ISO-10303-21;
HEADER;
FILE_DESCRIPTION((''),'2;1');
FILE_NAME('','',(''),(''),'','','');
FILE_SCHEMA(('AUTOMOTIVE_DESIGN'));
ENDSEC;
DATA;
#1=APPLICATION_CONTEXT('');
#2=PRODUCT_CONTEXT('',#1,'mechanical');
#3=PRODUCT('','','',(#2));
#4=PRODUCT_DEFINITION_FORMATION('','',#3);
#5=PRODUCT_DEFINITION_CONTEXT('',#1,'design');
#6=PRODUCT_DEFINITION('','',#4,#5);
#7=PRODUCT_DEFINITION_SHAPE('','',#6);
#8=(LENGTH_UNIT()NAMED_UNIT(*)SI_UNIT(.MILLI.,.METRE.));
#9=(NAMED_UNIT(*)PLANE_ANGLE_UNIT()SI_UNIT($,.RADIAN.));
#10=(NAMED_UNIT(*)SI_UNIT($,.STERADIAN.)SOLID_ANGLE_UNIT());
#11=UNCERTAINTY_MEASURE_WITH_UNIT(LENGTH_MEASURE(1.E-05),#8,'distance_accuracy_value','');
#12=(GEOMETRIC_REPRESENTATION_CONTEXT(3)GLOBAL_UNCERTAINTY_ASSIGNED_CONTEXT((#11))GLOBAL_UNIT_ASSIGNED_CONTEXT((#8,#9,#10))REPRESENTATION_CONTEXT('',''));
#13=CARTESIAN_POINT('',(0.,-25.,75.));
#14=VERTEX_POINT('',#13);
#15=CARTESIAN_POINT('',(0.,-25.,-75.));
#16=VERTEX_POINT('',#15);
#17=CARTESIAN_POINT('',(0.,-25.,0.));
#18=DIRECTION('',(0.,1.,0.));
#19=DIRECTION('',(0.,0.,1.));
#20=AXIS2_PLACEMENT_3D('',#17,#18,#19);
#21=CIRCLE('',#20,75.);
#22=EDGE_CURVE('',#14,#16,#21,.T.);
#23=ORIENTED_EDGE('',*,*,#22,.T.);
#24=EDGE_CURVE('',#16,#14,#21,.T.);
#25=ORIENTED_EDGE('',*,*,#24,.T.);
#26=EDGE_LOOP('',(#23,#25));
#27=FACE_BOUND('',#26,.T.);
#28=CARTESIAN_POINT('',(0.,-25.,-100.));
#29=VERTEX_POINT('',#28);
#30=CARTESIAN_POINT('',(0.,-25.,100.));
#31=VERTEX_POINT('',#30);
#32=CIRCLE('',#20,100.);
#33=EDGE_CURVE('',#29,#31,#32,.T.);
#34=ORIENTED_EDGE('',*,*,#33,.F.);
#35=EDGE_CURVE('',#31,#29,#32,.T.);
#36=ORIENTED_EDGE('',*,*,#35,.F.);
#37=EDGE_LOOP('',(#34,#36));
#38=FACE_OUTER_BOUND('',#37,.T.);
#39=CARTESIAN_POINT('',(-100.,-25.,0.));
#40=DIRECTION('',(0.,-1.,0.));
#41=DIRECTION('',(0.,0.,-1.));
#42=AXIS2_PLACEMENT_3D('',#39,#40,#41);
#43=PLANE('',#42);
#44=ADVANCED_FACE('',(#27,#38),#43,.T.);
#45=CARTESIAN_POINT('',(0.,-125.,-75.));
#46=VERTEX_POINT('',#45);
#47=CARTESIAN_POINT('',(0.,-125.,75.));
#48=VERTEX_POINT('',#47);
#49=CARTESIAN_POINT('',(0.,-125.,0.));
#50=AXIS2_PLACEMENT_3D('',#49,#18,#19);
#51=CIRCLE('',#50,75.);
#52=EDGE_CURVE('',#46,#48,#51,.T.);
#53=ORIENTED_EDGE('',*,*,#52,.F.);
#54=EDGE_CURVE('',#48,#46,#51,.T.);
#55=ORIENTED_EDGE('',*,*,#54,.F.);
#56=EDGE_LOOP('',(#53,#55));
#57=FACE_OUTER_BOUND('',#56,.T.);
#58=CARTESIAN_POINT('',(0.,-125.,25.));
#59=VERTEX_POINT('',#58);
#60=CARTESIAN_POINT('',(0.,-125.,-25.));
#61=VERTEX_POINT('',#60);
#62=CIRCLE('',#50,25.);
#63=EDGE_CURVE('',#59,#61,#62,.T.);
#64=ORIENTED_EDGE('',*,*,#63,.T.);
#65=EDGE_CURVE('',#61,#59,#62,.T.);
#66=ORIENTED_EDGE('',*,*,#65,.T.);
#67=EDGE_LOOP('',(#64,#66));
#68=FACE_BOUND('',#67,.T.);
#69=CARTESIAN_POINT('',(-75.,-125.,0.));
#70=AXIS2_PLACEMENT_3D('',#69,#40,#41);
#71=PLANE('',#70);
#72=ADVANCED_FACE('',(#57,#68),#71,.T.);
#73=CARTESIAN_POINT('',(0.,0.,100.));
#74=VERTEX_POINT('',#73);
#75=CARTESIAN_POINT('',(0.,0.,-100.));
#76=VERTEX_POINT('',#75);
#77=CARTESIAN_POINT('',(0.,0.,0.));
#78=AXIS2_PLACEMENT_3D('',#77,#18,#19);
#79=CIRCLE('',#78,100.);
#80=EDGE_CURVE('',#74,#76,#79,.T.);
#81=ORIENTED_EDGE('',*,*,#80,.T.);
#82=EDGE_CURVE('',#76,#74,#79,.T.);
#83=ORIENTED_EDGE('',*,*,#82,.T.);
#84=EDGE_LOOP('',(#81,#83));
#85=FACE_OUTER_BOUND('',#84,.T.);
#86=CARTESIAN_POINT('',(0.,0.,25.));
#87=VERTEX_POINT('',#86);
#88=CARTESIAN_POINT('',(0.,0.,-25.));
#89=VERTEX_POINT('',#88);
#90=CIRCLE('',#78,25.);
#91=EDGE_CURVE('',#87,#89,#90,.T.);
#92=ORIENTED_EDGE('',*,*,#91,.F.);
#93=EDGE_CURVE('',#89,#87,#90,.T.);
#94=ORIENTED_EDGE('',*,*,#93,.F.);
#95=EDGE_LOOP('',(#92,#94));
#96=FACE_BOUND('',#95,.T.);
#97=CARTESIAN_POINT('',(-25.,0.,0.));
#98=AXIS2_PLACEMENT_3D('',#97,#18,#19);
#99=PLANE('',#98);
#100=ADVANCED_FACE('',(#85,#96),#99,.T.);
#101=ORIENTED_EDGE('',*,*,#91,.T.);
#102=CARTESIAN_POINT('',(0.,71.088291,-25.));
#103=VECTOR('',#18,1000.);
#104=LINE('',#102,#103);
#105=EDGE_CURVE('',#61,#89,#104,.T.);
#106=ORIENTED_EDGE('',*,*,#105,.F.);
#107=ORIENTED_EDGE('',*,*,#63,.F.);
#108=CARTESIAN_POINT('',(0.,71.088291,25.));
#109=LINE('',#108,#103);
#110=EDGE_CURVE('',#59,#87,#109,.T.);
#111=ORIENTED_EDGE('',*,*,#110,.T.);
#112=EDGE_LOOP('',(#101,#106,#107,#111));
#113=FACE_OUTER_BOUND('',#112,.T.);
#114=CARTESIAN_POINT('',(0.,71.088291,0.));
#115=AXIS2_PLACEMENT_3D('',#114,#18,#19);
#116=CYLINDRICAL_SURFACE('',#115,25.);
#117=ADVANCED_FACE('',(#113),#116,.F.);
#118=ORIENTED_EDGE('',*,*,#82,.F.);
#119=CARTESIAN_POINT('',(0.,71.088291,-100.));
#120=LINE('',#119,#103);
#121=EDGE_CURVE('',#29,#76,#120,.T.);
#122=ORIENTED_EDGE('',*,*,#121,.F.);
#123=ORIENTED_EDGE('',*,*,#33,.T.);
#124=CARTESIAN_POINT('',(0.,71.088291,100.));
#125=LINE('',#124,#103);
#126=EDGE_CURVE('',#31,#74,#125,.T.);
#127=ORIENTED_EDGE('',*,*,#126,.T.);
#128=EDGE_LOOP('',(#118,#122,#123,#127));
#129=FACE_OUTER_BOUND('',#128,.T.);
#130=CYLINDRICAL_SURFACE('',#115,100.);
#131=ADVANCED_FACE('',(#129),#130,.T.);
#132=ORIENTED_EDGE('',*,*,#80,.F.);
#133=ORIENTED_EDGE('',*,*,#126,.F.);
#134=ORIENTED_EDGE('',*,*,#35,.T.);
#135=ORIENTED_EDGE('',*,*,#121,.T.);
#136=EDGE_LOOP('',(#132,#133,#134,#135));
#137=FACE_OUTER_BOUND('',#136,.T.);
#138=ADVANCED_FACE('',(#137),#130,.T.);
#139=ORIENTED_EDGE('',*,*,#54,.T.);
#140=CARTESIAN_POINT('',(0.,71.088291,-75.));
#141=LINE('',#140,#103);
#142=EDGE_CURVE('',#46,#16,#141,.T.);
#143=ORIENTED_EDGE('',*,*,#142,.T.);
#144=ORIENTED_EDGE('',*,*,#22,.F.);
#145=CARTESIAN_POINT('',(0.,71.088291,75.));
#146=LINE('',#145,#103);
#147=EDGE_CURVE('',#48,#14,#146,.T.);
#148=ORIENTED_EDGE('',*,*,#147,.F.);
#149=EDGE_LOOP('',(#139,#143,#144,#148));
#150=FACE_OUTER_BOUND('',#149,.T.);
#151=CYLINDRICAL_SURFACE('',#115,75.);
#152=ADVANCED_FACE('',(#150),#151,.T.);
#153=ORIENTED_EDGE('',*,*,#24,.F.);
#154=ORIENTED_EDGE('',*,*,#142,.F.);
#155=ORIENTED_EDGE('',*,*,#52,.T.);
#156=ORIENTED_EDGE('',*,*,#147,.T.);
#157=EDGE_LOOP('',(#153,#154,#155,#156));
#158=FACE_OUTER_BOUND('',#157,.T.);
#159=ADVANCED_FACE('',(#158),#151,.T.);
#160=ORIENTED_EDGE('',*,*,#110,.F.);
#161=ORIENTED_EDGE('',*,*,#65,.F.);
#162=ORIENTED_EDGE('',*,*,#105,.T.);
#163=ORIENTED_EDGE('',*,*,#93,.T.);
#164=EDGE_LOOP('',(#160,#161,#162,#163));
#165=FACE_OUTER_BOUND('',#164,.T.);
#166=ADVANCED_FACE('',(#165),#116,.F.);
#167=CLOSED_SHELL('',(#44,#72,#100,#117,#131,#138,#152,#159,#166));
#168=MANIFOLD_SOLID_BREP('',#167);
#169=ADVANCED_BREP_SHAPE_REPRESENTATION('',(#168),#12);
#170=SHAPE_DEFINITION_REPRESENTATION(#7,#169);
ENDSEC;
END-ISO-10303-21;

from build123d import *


with BuildPart() as part:
    # Sketch1 → Revolve1 (revolve)
    with BuildSketch(Plane.XY, mode=Mode.PRIVATE) as revolve1_sk:
        Polygon((-25, 0), (-100, 0), (-100, -25), (-75, -25), (-75, -125), (-25, -125), align=None)
    revolve(revolve1_sk.sketch.rotate(Axis((0, 71.088290965, 0), (0, -1, 0)), 270), axis=Axis((0, 71.088290965, 0), (0, -1, 0)))


solid = part.part
